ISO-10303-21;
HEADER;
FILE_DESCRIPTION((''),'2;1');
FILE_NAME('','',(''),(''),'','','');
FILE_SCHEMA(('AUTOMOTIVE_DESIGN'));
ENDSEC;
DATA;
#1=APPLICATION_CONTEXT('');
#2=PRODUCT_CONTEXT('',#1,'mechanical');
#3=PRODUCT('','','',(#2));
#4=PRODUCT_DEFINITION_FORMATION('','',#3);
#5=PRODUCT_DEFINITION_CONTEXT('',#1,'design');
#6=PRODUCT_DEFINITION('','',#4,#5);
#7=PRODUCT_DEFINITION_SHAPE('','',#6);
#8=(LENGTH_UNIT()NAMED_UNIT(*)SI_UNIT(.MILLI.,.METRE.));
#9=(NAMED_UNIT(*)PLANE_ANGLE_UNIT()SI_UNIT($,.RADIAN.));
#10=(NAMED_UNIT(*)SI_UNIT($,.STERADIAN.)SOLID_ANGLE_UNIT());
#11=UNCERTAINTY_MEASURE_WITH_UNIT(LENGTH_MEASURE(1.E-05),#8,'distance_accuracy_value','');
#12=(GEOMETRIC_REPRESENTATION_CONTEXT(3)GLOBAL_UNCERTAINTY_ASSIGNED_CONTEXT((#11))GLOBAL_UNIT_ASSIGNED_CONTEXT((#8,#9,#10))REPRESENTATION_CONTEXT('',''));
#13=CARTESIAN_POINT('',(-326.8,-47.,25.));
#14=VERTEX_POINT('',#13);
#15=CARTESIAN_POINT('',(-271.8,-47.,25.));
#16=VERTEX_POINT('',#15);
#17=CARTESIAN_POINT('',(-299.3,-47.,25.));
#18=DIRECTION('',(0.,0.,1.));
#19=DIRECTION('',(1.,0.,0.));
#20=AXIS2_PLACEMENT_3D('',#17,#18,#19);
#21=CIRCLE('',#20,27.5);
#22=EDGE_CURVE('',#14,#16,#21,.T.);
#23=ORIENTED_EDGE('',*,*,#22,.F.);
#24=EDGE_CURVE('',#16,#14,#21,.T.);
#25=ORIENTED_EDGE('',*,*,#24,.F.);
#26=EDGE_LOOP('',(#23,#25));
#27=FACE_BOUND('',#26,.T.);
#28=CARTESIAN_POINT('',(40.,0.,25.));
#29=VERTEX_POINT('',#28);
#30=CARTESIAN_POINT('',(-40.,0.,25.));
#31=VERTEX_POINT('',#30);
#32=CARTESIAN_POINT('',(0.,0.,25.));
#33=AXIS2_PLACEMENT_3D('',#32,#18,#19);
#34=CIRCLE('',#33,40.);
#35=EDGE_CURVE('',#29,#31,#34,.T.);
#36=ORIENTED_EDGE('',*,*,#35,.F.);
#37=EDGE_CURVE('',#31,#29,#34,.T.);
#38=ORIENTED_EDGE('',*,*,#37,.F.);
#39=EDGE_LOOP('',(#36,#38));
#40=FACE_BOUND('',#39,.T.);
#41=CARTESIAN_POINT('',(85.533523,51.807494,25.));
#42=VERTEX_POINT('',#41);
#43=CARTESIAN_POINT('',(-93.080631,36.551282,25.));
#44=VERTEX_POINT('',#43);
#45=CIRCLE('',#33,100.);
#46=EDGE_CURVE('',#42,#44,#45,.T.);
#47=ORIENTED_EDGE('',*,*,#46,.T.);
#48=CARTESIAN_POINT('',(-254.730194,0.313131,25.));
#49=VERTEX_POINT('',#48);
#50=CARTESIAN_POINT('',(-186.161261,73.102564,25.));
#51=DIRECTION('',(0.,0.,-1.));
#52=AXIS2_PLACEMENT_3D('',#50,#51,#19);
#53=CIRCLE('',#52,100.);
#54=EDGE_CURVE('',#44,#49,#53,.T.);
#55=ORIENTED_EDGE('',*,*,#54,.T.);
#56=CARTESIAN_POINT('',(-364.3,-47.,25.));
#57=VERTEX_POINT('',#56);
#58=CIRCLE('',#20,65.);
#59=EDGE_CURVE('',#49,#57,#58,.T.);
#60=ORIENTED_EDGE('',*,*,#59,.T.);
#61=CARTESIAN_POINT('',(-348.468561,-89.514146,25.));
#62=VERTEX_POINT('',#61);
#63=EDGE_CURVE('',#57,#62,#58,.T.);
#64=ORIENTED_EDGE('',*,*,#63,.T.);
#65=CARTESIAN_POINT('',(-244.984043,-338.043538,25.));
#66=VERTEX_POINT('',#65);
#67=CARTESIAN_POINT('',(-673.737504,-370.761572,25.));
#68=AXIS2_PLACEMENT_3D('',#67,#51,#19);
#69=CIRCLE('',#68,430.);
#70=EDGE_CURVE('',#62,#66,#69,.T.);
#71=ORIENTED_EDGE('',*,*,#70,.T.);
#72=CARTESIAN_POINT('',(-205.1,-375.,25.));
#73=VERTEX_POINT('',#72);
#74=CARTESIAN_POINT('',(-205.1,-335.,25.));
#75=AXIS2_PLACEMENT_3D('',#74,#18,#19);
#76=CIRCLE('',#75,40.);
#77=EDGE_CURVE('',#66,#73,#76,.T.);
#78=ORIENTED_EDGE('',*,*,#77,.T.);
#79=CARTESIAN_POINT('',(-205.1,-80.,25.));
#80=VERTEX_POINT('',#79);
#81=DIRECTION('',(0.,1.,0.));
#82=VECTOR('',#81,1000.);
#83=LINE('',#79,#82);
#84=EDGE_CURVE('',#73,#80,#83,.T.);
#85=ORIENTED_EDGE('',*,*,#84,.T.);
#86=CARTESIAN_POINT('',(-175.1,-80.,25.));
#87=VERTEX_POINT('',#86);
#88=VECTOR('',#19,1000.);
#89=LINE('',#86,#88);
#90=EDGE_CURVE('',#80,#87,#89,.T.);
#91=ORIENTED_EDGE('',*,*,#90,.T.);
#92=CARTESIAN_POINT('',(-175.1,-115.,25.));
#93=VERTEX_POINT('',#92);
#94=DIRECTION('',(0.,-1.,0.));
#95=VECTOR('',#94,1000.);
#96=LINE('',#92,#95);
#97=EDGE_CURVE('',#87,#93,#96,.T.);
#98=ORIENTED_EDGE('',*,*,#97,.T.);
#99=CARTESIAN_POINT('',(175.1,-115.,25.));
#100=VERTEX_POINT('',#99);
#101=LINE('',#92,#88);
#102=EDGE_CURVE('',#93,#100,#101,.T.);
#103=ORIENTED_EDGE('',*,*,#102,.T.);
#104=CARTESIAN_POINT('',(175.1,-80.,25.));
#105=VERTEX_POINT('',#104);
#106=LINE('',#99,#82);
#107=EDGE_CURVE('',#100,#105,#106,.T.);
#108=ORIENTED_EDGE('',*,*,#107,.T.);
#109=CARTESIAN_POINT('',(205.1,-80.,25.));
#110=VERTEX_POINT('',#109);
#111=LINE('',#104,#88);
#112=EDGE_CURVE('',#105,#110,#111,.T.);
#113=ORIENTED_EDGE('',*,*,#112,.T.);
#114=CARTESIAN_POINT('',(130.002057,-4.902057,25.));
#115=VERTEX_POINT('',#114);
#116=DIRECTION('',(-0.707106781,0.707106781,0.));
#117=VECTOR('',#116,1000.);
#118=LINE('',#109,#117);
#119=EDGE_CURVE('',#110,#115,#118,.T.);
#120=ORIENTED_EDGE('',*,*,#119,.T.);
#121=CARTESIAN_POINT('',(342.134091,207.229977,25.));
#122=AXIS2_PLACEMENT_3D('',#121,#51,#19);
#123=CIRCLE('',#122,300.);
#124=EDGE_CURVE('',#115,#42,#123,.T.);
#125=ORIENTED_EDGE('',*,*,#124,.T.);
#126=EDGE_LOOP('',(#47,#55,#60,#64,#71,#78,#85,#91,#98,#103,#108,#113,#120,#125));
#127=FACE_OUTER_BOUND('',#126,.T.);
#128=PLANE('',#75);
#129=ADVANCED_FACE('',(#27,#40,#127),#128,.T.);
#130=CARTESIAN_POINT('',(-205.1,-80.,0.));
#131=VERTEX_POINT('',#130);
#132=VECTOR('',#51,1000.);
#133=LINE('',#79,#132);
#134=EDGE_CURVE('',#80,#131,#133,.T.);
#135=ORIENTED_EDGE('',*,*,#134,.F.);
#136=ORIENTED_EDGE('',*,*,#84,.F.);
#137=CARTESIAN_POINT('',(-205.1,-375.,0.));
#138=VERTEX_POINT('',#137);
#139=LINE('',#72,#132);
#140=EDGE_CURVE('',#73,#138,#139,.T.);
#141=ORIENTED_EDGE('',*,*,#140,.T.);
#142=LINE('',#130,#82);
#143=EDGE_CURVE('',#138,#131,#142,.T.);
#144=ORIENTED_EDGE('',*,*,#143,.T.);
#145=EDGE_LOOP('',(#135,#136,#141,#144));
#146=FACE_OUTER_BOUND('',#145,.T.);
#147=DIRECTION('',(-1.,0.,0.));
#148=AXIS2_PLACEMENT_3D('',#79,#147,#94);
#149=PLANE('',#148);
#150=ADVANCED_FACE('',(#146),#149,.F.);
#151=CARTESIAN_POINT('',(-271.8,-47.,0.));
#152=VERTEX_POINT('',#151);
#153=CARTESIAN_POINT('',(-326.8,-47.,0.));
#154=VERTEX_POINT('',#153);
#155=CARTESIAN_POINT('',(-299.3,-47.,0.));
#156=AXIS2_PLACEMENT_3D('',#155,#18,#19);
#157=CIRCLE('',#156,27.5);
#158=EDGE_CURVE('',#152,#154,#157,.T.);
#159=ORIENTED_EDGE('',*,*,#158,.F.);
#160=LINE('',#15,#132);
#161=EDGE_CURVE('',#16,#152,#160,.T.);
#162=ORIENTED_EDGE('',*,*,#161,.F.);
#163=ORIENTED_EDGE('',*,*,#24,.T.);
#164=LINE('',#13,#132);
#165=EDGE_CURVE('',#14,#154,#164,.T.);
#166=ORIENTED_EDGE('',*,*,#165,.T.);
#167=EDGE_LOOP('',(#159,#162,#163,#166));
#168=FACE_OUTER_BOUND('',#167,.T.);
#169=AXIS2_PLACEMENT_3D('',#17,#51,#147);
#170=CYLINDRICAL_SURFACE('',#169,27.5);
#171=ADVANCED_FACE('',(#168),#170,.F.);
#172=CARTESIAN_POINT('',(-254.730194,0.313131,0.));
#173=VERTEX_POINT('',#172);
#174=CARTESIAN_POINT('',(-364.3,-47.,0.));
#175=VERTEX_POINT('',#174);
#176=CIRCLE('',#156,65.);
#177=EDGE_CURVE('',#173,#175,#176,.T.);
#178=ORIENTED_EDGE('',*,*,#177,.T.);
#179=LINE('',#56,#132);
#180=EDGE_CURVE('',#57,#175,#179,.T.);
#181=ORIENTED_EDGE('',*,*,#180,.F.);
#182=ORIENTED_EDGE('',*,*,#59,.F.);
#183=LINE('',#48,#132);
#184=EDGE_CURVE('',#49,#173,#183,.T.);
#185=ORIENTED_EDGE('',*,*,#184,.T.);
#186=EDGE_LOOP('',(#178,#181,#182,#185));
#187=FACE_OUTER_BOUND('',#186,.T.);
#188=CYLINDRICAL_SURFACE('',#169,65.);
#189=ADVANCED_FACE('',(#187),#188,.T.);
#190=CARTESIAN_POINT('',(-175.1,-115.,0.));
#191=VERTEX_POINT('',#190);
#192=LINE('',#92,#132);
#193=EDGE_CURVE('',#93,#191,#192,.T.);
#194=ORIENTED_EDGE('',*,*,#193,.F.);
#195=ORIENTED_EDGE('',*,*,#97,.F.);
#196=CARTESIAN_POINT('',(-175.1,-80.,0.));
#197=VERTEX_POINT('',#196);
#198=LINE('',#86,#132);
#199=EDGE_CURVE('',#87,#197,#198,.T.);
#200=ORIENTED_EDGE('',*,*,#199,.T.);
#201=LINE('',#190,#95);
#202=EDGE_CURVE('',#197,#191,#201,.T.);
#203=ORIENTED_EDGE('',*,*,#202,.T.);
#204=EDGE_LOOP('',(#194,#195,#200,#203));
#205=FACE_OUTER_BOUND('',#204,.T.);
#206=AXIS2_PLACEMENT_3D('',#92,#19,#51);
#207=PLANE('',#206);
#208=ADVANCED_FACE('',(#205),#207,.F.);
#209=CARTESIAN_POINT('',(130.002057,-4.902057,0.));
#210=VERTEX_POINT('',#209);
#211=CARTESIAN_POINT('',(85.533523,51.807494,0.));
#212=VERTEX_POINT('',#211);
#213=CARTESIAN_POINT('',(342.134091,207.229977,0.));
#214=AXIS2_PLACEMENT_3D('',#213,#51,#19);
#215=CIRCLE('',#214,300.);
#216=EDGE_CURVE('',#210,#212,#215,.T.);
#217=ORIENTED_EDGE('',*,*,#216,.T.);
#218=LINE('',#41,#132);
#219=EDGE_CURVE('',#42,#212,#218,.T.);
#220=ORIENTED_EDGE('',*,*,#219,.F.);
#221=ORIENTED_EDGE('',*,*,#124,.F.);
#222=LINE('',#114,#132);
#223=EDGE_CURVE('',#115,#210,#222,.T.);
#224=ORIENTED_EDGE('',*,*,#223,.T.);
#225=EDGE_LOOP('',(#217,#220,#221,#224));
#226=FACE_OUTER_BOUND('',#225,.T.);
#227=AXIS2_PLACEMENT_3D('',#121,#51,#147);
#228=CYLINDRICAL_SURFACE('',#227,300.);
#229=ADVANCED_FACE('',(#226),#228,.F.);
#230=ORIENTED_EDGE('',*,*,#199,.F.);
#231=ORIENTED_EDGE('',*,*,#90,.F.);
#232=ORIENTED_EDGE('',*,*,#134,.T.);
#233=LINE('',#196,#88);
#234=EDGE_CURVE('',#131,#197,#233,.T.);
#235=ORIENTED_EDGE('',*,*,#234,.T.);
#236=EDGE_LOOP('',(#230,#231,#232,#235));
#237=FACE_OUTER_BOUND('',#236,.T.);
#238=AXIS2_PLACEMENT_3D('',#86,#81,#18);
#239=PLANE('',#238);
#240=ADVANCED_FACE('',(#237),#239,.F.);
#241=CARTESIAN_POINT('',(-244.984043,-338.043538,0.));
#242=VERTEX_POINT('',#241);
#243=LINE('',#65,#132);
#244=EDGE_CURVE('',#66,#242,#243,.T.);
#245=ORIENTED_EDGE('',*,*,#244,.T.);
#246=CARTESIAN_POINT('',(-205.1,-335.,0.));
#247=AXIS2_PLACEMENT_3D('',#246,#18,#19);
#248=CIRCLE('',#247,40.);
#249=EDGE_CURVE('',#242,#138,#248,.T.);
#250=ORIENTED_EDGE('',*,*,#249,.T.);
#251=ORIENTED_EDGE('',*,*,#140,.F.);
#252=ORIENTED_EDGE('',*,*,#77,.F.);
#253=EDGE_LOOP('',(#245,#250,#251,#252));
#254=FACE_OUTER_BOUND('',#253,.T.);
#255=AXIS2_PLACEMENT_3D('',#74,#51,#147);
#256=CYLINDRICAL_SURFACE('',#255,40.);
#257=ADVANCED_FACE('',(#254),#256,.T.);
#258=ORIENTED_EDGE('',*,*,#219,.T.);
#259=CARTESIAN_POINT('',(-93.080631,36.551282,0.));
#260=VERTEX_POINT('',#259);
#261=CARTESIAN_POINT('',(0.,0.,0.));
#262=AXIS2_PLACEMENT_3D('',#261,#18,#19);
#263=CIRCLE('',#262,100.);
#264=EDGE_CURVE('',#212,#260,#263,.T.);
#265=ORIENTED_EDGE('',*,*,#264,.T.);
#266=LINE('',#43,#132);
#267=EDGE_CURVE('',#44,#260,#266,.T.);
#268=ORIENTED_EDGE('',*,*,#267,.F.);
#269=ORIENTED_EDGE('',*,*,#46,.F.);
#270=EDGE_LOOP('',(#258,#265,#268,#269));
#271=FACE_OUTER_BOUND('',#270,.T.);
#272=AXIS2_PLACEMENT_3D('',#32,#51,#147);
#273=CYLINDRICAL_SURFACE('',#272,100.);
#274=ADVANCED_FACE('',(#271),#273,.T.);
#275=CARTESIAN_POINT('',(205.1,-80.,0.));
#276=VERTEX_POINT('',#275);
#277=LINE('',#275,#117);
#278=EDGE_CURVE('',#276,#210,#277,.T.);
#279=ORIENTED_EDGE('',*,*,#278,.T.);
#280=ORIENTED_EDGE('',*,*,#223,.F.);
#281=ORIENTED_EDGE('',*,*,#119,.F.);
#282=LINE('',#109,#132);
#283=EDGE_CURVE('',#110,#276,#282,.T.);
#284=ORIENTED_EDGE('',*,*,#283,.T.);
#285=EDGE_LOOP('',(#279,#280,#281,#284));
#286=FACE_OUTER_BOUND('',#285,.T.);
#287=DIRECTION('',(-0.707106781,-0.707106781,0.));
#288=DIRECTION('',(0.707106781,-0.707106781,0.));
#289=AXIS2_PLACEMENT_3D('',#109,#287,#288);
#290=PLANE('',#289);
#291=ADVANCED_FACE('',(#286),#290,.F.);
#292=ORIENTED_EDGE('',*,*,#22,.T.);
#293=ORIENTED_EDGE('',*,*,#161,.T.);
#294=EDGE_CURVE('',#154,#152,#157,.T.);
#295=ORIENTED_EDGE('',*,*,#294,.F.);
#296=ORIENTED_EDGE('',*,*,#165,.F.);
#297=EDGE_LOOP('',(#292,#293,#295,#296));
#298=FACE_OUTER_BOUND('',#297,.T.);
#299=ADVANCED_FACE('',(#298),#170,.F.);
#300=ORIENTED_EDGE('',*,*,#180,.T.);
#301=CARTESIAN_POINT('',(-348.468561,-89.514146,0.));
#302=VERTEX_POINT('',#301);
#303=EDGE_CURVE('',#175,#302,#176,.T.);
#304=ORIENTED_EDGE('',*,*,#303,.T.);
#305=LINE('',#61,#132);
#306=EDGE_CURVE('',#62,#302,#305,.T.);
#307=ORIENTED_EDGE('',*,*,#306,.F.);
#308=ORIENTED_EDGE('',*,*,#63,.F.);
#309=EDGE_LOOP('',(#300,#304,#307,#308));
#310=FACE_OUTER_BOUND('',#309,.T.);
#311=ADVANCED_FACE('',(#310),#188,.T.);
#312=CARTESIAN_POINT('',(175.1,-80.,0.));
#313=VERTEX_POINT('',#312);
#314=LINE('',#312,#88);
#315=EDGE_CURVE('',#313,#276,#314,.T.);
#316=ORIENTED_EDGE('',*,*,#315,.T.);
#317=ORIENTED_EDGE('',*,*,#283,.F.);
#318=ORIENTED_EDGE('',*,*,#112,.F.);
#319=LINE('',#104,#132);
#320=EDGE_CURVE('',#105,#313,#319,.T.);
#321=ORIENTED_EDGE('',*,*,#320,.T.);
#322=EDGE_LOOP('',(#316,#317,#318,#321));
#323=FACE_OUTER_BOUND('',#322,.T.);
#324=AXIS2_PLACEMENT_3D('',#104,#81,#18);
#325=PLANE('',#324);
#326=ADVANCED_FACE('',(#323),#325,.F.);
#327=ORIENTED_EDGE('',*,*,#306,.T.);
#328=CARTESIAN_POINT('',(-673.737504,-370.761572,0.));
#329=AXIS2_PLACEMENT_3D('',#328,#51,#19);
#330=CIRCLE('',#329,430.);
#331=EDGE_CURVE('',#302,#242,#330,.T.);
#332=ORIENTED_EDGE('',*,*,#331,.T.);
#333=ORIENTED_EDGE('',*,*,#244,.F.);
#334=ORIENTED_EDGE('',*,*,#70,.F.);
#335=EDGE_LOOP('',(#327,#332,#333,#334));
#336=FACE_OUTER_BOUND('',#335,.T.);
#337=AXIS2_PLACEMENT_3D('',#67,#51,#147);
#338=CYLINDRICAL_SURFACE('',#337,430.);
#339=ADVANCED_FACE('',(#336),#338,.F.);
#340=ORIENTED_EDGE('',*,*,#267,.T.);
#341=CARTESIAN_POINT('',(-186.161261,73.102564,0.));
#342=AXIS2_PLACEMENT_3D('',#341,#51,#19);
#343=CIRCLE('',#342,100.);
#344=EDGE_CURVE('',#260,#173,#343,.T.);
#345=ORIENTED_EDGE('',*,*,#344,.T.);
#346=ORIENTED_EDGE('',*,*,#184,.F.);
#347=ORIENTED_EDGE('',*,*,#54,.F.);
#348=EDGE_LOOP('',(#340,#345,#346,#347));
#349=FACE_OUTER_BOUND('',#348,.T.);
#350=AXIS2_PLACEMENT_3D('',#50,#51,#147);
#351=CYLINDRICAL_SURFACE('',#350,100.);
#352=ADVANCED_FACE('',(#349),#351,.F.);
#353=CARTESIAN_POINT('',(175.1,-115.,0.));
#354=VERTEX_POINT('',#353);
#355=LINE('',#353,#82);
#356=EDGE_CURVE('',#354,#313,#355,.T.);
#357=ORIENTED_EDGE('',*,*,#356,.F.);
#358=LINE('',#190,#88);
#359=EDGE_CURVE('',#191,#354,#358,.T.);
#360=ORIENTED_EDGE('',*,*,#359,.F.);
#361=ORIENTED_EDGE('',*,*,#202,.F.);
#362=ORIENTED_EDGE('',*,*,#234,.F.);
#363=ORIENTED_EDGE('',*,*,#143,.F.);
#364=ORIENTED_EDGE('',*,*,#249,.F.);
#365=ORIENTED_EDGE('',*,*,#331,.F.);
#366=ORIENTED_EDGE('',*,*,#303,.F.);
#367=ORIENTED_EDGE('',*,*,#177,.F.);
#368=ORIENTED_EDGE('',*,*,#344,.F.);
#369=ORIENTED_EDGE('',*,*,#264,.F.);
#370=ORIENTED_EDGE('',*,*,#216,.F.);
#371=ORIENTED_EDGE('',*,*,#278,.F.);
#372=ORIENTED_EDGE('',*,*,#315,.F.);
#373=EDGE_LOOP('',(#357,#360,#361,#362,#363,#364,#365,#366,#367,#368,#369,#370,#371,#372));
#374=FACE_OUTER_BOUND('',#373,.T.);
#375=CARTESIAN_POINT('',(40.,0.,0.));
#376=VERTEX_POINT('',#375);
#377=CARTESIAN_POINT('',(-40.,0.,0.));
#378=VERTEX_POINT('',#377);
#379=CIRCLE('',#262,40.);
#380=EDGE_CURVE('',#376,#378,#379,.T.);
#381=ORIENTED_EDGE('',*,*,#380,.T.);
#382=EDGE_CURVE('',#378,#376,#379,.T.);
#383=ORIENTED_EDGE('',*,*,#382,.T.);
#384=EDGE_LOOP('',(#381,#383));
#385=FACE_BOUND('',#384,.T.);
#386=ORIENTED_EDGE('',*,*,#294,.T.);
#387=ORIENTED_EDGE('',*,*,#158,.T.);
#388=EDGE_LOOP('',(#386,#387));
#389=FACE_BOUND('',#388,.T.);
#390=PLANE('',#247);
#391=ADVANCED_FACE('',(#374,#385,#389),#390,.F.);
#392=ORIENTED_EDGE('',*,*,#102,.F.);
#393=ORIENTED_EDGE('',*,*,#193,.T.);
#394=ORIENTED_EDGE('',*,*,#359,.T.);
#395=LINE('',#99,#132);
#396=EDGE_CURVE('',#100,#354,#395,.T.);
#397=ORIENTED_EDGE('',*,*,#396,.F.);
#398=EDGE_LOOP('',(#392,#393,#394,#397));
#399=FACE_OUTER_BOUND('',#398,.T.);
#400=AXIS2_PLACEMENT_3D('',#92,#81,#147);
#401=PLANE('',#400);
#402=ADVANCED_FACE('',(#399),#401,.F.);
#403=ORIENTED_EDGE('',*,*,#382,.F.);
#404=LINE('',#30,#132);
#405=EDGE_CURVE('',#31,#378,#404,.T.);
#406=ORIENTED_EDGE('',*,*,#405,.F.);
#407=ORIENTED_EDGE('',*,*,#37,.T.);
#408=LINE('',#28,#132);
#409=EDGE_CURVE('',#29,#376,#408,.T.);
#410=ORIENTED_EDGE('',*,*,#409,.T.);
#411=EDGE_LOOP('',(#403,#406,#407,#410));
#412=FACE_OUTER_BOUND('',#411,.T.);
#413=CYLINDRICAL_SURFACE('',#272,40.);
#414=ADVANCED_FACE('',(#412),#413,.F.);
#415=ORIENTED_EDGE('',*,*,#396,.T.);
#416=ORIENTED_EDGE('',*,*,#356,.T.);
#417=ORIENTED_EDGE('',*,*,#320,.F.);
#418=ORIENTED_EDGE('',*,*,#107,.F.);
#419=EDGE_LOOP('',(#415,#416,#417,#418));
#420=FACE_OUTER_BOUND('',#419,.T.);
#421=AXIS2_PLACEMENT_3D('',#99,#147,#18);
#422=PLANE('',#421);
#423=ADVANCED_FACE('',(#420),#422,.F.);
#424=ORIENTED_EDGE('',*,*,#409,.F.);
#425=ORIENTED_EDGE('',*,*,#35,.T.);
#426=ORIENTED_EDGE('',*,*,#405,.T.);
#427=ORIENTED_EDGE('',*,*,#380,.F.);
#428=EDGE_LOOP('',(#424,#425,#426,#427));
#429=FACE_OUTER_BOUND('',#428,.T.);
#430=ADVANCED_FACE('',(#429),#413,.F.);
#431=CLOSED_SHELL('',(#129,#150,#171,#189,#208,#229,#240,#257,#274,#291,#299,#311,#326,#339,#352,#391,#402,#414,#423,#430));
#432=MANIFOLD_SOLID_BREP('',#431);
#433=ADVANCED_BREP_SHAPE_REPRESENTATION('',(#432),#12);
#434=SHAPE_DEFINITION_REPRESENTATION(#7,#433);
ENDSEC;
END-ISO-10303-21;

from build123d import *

# Parameters (mm, degrees)
SKETCH1_R           = 40
SKETCH1_R_2         = 27.5
BOSS_EXTRUDE1_DEPTH = 25


with BuildPart() as part:
    # Sketch1 → Boss-Extrude1 (new body)
    with BuildSketch(Plane.XY):
        with BuildLine():
            Line((-175.1, -115), (175.1, -115))
            Line((175.1, -115), (175.1, -80))
            Line((175.1, -80), (205.1, -80))
            Line((205.1, -80), (130.002057063, -4.902057063))
            ThreePointArc((130.002057063, -4.902057063), (106.058771733, 22.112599839), (85.533522855, 51.807494323))
            ThreePointArc((85.533522855, 51.807494323), (-8.510447338, 99.637203323), (-93.080630623, 36.551281821))
            ThreePointArc((-93.080630623, 36.551281821), (-164.286464639, -24.475575679), (-254.730193824, 0.313131132))
            ThreePointArc((-254.730193824, 0.313131132), (-344.272458908, -0.069434909), (-348.468561101, -89.514145872))
            ThreePointArc((-348.468561101, -89.514145872), (-276.775086195, -205.471406239), (-244.984042874, -338.043538078))
            ThreePointArc((-244.984042874, -338.043538078), (-232.286931391, -364.340599202), (-205.1, -375))
            Line((-205.1, -375), (-205.1, -80))
            Line((-205.1, -80), (-175.1, -80))
            Line((-175.1, -80), (-175.1, -115))
        make_face()
        Circle(SKETCH1_R, mode=Mode.SUBTRACT)
        with Locations((-299.3, -47)):
            Circle(SKETCH1_R_2, mode=Mode.SUBTRACT)
    extrude(amount=BOSS_EXTRUDE1_DEPTH)


solid = part.part
